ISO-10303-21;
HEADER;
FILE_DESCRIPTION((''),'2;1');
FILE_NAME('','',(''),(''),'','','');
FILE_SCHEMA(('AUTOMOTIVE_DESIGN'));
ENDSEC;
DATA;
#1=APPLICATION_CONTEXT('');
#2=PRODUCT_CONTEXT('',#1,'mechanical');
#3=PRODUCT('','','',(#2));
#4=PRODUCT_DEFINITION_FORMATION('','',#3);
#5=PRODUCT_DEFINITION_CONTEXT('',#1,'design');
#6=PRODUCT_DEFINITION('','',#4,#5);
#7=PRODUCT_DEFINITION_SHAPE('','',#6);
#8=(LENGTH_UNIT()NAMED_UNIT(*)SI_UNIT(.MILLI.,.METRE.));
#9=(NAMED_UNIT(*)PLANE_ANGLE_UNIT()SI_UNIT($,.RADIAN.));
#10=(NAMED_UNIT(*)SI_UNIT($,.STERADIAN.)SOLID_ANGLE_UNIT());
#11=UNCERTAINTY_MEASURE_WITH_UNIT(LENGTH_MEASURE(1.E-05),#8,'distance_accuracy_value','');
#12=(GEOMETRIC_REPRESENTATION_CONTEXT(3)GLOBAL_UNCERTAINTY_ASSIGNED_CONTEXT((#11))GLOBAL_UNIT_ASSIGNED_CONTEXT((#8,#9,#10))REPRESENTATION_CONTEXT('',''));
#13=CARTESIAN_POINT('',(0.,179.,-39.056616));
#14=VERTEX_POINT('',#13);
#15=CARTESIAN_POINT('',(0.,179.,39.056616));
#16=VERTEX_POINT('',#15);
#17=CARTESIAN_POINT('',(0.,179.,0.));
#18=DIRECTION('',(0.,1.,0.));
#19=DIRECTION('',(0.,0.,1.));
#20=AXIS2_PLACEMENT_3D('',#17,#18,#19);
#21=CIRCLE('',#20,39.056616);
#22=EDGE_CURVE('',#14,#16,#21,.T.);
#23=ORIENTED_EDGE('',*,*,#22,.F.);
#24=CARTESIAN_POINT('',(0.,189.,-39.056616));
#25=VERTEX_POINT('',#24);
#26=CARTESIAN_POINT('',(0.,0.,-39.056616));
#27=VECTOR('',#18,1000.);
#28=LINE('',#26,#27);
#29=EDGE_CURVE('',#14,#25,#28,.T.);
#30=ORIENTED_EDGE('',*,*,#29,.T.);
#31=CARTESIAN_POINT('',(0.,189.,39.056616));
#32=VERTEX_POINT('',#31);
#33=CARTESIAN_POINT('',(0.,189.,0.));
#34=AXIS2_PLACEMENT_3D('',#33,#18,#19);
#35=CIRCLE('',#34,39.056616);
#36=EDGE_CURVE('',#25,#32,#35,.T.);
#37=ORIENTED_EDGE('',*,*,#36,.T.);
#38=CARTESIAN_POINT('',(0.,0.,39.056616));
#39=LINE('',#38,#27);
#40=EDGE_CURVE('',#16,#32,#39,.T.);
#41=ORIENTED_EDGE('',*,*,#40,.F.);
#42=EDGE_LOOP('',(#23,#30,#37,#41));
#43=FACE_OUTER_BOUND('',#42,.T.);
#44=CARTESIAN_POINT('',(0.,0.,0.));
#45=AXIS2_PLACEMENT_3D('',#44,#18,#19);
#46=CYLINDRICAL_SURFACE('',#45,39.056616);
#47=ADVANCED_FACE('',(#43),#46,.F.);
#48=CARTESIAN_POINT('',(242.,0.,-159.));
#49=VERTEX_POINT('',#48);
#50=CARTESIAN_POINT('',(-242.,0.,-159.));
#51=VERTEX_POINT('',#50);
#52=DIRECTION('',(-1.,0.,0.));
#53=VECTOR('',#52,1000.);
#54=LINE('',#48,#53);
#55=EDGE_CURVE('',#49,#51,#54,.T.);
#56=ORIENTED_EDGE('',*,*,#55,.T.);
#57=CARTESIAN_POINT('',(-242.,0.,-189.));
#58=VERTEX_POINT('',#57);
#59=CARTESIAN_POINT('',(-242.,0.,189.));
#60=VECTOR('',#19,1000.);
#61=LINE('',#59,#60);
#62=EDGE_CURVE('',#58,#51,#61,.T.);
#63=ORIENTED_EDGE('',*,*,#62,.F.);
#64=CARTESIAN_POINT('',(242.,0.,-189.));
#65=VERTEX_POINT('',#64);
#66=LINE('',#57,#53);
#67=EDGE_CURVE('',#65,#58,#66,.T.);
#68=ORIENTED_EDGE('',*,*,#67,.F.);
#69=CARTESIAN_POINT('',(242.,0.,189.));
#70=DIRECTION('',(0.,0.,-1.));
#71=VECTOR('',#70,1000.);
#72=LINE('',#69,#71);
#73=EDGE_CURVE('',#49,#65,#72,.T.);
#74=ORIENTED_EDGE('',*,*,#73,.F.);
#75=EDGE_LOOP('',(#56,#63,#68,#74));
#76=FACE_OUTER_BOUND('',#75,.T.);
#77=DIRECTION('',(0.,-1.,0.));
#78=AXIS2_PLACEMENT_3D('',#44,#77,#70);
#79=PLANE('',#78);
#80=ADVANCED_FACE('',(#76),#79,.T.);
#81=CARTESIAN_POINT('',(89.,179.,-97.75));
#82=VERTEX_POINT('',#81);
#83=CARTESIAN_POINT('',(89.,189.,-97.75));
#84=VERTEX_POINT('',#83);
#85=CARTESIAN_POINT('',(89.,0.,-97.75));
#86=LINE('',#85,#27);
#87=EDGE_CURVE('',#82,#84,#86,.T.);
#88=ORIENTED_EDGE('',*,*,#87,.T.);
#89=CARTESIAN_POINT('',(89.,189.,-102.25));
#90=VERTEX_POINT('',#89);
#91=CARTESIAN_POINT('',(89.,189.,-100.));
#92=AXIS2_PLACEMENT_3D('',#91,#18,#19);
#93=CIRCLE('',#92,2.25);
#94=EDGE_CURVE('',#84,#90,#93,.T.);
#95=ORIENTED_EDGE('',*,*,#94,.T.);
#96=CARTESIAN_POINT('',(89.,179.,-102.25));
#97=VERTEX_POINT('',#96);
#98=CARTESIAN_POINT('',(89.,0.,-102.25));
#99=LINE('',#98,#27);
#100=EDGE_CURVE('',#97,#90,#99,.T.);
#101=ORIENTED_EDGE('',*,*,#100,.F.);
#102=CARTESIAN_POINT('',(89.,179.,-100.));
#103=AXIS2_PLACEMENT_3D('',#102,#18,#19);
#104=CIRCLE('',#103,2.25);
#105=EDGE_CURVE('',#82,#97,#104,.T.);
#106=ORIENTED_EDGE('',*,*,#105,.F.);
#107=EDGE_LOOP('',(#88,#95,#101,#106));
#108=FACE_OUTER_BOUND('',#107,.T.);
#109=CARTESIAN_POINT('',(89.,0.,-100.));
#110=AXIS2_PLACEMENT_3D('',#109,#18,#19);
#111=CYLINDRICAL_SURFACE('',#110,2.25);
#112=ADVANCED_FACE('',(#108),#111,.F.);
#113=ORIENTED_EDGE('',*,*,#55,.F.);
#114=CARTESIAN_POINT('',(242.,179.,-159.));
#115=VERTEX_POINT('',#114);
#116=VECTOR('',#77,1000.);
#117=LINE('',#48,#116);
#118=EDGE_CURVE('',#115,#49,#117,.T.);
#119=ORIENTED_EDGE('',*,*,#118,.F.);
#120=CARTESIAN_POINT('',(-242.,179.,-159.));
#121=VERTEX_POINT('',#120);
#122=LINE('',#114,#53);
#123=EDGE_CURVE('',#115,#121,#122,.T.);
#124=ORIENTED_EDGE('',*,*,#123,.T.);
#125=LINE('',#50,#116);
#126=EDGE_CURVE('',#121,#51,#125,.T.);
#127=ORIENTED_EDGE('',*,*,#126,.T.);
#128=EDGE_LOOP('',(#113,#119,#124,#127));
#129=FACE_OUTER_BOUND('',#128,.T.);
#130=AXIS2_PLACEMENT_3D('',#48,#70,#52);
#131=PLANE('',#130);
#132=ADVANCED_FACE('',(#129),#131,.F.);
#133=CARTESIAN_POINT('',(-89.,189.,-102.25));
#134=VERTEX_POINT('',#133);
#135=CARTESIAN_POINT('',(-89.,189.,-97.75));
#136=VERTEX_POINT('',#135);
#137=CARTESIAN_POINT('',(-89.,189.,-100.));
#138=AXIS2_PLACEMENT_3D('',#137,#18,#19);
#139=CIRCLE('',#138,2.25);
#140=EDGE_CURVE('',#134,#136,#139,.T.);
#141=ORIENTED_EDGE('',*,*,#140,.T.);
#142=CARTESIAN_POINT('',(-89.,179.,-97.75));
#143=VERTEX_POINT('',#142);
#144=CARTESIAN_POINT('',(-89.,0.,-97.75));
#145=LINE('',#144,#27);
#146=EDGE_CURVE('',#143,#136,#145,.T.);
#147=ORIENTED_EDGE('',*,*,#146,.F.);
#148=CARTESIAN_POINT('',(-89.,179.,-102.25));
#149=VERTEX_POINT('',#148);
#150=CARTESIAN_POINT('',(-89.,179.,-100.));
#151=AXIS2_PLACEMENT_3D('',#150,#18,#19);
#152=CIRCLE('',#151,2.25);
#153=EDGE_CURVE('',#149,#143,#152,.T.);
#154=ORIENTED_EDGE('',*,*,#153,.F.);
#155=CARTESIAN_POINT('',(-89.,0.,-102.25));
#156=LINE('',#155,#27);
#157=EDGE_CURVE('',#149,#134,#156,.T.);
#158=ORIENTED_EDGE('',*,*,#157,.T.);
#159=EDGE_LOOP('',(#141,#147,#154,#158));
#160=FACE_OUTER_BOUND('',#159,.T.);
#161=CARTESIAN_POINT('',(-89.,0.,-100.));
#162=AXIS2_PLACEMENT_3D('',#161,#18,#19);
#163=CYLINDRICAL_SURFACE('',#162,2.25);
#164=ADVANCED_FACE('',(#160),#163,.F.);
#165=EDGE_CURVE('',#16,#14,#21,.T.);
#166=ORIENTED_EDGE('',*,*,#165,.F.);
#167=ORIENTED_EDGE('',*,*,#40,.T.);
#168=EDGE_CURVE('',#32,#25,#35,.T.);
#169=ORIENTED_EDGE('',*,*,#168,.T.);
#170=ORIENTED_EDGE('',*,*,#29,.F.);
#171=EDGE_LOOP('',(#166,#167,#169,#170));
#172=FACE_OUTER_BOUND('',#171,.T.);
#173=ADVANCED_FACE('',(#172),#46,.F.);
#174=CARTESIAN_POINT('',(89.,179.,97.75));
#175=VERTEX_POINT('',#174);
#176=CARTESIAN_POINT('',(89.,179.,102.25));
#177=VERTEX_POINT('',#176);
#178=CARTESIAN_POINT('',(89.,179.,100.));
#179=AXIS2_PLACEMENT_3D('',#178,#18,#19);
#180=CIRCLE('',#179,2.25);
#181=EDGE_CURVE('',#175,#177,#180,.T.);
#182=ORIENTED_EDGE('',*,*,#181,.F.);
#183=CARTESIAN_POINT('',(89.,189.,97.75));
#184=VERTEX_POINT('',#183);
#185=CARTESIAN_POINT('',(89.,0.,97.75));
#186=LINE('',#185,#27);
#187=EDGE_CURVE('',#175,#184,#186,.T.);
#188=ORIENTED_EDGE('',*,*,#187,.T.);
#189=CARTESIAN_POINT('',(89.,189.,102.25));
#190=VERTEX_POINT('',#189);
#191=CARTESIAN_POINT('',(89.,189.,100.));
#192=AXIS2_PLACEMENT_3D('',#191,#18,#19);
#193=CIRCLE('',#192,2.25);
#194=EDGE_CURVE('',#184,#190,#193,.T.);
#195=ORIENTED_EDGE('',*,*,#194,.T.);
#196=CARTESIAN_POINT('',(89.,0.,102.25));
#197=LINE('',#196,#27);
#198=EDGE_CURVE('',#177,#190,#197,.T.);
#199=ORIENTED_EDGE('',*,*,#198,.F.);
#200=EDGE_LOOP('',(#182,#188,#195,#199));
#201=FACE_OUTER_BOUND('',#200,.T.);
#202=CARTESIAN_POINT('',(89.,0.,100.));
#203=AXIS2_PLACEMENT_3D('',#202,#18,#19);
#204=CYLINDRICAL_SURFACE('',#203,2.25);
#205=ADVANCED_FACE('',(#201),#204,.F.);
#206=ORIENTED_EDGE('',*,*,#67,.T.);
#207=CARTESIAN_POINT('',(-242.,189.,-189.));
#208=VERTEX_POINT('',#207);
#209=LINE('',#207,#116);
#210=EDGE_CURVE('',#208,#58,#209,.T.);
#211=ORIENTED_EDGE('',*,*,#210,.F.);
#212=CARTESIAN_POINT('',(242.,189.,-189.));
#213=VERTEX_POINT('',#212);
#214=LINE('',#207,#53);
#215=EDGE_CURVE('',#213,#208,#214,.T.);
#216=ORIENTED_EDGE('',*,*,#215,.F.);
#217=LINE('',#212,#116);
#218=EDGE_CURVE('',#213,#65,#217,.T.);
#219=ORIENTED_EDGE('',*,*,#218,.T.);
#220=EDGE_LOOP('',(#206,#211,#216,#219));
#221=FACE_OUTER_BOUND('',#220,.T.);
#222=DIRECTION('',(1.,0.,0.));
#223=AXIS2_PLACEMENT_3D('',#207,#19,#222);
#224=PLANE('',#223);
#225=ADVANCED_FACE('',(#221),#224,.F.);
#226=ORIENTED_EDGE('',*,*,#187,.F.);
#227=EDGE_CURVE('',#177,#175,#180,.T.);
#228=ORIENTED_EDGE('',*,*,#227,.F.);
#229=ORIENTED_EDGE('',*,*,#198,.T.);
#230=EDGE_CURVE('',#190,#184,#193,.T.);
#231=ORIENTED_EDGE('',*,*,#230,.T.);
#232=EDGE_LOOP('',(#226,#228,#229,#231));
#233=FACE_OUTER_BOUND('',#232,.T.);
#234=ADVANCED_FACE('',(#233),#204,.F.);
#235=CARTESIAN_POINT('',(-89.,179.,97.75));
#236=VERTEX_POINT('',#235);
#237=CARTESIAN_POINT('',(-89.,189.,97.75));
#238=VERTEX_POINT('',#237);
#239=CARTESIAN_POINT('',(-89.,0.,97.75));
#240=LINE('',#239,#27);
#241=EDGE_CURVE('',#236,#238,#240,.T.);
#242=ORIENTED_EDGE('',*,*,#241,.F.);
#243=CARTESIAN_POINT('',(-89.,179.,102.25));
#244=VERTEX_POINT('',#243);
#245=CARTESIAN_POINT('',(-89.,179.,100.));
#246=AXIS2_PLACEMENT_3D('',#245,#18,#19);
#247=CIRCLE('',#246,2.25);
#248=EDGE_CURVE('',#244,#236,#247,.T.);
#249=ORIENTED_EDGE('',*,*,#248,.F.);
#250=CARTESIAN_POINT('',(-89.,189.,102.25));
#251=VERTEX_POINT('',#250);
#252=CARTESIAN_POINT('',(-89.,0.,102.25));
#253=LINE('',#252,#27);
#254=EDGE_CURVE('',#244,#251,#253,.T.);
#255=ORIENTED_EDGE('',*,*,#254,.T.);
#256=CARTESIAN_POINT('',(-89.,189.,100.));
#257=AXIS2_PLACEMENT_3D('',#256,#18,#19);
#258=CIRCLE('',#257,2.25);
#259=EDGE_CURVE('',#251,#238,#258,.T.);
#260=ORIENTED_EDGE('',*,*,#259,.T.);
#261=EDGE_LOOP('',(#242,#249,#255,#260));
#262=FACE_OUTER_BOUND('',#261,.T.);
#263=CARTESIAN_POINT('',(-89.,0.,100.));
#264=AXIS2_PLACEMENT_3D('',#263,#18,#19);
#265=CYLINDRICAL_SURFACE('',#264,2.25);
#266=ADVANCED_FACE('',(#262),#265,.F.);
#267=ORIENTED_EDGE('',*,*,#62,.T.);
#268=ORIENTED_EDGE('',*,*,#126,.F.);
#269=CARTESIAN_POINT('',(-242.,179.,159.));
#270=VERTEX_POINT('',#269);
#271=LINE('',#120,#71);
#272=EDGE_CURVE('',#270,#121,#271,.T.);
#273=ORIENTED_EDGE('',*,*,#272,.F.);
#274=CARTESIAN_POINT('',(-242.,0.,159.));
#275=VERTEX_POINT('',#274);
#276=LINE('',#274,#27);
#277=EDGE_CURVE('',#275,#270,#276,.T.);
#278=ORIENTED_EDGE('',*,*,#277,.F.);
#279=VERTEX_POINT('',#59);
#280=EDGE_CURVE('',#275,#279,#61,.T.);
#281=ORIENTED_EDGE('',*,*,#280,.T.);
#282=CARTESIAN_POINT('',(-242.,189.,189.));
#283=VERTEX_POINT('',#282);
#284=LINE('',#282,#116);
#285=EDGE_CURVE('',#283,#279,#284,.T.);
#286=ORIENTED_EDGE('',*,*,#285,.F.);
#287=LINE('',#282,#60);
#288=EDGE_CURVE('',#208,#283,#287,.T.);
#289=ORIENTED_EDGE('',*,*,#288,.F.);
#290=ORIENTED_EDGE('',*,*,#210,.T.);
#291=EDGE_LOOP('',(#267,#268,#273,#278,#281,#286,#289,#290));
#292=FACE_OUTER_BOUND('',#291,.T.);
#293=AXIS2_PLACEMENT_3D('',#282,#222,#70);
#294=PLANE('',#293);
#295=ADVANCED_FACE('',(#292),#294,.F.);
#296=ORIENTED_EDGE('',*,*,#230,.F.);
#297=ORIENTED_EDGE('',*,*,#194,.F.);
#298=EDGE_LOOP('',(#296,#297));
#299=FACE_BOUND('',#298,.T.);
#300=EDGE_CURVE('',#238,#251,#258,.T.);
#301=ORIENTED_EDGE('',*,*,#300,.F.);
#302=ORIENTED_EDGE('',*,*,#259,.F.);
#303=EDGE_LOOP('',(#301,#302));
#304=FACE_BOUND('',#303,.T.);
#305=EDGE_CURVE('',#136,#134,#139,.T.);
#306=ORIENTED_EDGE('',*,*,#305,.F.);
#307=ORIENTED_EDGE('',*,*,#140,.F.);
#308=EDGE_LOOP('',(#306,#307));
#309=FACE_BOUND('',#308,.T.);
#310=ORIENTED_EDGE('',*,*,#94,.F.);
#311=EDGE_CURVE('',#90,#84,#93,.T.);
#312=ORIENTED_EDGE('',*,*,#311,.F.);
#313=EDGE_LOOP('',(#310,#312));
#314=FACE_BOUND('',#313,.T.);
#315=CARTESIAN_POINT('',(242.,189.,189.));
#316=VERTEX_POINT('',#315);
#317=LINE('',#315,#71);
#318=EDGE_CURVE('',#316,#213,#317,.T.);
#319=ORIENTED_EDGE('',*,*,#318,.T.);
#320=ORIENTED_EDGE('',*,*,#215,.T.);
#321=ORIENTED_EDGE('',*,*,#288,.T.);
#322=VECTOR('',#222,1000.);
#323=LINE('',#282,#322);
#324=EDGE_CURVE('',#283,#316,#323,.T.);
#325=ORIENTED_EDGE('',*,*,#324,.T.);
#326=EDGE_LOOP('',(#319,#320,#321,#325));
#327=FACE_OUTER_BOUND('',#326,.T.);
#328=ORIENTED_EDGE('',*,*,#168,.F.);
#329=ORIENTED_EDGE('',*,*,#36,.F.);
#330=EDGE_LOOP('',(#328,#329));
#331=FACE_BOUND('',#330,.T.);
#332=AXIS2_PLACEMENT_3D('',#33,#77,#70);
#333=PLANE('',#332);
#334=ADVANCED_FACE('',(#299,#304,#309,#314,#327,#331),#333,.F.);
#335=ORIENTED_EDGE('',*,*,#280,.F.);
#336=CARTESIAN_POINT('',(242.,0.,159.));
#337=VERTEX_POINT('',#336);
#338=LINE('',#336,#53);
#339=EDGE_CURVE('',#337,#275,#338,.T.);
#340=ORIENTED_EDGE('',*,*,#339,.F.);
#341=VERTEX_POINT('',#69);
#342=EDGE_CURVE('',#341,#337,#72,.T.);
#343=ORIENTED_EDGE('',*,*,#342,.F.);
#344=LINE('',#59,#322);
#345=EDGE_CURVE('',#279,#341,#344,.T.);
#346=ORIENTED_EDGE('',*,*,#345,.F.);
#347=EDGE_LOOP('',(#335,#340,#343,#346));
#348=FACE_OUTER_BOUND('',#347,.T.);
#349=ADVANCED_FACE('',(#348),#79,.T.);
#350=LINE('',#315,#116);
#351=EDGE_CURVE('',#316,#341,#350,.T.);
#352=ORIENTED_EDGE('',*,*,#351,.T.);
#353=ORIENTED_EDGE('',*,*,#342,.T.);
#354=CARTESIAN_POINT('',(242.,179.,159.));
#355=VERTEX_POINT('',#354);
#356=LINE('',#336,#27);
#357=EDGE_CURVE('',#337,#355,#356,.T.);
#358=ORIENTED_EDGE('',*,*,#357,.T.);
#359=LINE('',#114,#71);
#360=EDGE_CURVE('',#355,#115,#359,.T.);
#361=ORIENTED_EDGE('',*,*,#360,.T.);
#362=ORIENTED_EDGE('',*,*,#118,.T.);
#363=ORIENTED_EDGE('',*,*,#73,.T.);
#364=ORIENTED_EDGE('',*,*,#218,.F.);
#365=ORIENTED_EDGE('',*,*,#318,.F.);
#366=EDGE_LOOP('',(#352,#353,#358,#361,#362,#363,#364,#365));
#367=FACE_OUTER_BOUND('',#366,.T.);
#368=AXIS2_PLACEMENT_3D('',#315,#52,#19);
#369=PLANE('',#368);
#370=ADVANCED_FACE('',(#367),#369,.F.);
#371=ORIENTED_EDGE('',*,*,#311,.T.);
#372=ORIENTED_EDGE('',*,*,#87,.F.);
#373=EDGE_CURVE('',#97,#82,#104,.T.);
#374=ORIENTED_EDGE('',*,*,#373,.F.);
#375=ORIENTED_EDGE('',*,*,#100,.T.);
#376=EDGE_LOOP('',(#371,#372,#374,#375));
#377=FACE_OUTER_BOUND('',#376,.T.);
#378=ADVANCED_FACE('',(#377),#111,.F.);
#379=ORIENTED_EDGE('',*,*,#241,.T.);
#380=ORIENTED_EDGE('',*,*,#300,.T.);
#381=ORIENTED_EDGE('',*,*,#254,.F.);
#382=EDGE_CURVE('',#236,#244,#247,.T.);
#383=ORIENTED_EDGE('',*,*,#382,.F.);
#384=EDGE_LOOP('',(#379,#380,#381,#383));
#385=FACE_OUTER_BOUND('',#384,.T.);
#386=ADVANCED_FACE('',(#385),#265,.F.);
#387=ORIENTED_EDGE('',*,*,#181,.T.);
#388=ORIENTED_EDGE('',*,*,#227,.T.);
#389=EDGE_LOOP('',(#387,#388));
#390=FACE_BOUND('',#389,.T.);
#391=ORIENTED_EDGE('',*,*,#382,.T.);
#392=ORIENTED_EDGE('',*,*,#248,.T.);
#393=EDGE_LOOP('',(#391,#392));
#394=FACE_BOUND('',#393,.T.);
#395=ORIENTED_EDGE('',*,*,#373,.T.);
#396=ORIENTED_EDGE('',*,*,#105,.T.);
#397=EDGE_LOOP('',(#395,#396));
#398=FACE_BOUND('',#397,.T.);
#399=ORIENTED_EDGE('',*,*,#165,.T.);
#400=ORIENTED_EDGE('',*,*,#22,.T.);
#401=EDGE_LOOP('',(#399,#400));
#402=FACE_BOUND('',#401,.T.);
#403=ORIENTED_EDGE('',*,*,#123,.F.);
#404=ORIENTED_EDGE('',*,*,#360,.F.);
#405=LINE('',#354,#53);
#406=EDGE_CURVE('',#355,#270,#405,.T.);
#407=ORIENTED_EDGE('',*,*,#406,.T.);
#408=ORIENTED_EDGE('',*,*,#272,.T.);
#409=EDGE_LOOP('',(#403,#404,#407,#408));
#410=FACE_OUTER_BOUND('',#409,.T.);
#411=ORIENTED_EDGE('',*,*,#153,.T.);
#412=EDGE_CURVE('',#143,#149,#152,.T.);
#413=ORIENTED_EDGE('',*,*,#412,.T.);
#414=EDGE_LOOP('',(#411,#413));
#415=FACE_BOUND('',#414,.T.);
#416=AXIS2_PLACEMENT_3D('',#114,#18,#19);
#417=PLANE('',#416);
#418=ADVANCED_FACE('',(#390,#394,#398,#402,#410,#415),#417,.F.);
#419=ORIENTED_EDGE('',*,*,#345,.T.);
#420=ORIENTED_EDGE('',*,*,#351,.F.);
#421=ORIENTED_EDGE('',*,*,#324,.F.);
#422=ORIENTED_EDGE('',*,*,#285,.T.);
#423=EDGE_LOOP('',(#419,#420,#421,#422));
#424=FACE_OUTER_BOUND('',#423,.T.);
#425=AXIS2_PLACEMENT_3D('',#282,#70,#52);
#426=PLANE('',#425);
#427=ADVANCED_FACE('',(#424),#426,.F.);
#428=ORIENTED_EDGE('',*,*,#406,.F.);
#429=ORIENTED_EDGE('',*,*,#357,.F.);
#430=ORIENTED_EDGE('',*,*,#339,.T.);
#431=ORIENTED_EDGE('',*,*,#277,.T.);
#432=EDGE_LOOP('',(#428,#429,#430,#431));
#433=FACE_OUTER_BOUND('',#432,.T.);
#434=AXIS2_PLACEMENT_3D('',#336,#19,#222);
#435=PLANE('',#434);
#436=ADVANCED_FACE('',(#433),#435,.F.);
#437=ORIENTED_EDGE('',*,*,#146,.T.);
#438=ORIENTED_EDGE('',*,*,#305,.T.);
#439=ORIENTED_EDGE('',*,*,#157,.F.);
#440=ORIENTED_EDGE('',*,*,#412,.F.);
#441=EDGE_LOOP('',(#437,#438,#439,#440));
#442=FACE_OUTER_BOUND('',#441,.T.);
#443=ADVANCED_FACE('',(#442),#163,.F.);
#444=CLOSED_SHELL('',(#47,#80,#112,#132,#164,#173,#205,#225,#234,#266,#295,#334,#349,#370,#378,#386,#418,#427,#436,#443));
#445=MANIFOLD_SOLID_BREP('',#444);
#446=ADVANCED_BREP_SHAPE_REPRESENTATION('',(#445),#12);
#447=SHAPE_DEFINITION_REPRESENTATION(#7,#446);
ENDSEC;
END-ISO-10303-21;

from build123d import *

# Parameters (mm, degrees)
SKETCH1_W           = 484
SKETCH1_H           = 378
BOSS_EXTRUDE1_DEPTH = 189
SKETCH2_W           = 318
SKETCH2_H           = 179
CUT_EXTRUDE1_DEPTH  = 553.899629228
SKETCH3_R           = 2.25
SKETCH3_R_2         = 39.056616246
CUT_EXTRUDE2_DEPTH  = 361.563447953


with BuildPart() as part:
    # Sketch1 → Boss-Extrude1 (new body)
    with BuildSketch(Plane(origin=(0, 0, 0), x_dir=(1, 0, 0), z_dir=(0, 1, 0))):
        Rectangle(SKETCH1_W, SKETCH1_H)
    extrude(amount=BOSS_EXTRUDE1_DEPTH)

    # Sketch2 → Cut-Extrude1 (cut, through all)
    with BuildSketch(Plane.ZY.offset(242)):
        with Locations((0, 89.5)):
            Rectangle(SKETCH2_W, SKETCH2_H)
    extrude(amount=-CUT_EXTRUDE1_DEPTH, mode=Mode.SUBTRACT)

    # Sketch3 → Cut-Extrude2 (cut, through all)
    with BuildSketch(Plane(origin=(0, 189, 0), x_dir=(1, 0, 0), z_dir=(0, 1, 0))):
        with Locations(Location((-89, -100, 0), (0, 0, 270))):
            Circle(SKETCH3_R)
        with Locations(Location((89, -100, 0), (0, 0, 270))):
            Circle(SKETCH3_R)
        with Locations(Location((-89, 100, 0), (0, 0, 270))):
            Circle(SKETCH3_R)
        with Locations(Location((89, 100, 0), (0, 0, 270))):
            Circle(SKETCH3_R)
        with Locations(Location((0, 0, 0), (0, 0, 270))):
            Circle(SKETCH3_R_2)
    extrude(amount=-CUT_EXTRUDE2_DEPTH, mode=Mode.SUBTRACT)


solid = part.part
